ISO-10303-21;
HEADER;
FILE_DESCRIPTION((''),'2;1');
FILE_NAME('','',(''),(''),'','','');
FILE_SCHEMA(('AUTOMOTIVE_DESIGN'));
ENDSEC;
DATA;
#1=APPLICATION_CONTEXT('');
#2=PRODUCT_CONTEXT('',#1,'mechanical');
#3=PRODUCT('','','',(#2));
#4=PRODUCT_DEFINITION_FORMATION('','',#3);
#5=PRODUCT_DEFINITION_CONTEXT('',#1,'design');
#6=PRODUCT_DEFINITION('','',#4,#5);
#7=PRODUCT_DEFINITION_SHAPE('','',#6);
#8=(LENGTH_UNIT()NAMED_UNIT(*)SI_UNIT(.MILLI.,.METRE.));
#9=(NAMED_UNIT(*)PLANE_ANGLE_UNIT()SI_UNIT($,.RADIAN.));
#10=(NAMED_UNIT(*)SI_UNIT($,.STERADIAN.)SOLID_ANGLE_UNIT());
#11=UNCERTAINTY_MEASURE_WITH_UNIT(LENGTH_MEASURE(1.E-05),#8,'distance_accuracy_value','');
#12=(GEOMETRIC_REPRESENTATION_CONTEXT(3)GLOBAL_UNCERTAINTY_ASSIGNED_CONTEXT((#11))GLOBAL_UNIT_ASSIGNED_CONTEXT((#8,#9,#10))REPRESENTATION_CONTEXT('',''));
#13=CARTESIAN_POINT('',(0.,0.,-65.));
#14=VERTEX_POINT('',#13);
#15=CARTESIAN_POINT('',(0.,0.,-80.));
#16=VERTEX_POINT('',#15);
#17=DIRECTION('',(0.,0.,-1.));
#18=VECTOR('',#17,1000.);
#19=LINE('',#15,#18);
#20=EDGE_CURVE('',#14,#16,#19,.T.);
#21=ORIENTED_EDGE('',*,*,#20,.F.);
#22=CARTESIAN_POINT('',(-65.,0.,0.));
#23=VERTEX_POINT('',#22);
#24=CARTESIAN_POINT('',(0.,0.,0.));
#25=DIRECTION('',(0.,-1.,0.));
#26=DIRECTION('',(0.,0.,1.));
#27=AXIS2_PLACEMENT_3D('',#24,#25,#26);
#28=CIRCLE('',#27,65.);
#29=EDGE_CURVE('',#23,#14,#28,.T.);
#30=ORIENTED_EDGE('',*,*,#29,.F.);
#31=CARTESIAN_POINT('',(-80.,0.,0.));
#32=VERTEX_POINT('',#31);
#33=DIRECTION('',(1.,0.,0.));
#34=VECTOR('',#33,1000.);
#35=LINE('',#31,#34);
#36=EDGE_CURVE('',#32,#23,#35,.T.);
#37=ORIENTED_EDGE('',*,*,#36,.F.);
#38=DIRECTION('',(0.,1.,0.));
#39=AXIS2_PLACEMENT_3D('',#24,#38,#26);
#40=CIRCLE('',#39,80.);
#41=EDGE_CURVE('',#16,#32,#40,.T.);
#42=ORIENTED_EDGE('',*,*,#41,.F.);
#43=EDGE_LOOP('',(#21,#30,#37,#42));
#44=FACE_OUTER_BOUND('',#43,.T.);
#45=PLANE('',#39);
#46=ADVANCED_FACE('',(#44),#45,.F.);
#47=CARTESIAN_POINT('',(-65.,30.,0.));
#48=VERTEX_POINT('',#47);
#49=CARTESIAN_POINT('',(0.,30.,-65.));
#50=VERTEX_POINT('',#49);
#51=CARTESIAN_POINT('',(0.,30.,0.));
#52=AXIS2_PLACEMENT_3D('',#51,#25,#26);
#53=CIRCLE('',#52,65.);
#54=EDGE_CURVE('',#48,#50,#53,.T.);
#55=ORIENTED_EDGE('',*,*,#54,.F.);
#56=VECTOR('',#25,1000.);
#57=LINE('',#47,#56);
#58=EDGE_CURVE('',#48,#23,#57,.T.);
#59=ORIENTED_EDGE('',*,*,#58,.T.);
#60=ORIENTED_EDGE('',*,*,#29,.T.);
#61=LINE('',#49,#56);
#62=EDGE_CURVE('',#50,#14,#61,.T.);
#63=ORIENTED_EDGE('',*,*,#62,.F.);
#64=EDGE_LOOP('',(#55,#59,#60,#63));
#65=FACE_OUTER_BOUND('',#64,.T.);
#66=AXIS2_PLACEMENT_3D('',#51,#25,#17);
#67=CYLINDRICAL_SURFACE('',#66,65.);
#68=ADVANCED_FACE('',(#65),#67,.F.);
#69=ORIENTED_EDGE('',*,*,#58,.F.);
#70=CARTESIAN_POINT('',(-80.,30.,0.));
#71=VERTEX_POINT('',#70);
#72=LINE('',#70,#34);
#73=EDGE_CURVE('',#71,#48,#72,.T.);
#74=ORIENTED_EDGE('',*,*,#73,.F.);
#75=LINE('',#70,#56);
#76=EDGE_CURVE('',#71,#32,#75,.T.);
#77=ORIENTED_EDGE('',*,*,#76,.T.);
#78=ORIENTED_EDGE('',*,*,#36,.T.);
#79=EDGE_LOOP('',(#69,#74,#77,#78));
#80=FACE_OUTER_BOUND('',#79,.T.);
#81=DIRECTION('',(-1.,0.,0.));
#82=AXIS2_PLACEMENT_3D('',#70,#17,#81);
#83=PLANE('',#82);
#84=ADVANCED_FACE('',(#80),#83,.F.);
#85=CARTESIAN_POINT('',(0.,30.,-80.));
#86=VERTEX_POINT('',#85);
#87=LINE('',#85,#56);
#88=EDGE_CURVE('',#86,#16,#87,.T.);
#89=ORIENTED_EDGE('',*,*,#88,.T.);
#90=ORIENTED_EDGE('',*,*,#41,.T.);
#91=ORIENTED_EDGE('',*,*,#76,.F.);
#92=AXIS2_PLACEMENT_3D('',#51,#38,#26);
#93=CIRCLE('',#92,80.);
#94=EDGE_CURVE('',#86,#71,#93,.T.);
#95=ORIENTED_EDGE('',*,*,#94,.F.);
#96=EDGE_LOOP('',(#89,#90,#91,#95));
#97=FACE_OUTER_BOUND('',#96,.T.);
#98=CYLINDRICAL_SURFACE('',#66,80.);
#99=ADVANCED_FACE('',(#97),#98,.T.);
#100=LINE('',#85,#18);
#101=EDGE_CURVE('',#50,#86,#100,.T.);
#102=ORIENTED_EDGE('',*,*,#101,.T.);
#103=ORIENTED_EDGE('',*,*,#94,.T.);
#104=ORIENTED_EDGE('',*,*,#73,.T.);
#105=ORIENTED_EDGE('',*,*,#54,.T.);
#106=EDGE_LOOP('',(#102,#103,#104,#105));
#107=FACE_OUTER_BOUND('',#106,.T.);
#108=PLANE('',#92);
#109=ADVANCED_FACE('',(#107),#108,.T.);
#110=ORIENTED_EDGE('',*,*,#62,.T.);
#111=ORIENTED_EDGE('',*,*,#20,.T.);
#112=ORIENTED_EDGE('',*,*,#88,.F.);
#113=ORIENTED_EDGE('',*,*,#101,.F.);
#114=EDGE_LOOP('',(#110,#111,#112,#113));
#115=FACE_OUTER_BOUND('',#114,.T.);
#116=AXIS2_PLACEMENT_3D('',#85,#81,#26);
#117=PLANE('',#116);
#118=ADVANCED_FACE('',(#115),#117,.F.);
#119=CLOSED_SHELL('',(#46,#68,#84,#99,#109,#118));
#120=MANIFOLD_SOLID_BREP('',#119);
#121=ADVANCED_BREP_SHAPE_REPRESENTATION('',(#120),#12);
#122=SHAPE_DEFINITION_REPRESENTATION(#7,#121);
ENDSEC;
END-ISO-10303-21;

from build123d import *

# Parameters (mm, degrees)
EXTRUDE_1_DEPTH = 30


with BuildPart() as part:
    # 草图1 → 凸台-拉伸1 (new body)
    with BuildSketch(Plane(origin=(0, 0, 0), x_dir=(1, 0, 0), z_dir=(0, 1, 0))):
        with BuildLine():
            Line((-80, 0), (-65, 0))
            ThreePointArc((-65, 0), (-45.961940777, 45.961940777), (0, 65))
            Line((0, 65), (0, 80))
            ThreePointArc((0, 80), (-56.568542495, 56.568542495), (-80, 0))
        make_face()
    extrude(amount=EXTRUDE_1_DEPTH)


solid = part.part
